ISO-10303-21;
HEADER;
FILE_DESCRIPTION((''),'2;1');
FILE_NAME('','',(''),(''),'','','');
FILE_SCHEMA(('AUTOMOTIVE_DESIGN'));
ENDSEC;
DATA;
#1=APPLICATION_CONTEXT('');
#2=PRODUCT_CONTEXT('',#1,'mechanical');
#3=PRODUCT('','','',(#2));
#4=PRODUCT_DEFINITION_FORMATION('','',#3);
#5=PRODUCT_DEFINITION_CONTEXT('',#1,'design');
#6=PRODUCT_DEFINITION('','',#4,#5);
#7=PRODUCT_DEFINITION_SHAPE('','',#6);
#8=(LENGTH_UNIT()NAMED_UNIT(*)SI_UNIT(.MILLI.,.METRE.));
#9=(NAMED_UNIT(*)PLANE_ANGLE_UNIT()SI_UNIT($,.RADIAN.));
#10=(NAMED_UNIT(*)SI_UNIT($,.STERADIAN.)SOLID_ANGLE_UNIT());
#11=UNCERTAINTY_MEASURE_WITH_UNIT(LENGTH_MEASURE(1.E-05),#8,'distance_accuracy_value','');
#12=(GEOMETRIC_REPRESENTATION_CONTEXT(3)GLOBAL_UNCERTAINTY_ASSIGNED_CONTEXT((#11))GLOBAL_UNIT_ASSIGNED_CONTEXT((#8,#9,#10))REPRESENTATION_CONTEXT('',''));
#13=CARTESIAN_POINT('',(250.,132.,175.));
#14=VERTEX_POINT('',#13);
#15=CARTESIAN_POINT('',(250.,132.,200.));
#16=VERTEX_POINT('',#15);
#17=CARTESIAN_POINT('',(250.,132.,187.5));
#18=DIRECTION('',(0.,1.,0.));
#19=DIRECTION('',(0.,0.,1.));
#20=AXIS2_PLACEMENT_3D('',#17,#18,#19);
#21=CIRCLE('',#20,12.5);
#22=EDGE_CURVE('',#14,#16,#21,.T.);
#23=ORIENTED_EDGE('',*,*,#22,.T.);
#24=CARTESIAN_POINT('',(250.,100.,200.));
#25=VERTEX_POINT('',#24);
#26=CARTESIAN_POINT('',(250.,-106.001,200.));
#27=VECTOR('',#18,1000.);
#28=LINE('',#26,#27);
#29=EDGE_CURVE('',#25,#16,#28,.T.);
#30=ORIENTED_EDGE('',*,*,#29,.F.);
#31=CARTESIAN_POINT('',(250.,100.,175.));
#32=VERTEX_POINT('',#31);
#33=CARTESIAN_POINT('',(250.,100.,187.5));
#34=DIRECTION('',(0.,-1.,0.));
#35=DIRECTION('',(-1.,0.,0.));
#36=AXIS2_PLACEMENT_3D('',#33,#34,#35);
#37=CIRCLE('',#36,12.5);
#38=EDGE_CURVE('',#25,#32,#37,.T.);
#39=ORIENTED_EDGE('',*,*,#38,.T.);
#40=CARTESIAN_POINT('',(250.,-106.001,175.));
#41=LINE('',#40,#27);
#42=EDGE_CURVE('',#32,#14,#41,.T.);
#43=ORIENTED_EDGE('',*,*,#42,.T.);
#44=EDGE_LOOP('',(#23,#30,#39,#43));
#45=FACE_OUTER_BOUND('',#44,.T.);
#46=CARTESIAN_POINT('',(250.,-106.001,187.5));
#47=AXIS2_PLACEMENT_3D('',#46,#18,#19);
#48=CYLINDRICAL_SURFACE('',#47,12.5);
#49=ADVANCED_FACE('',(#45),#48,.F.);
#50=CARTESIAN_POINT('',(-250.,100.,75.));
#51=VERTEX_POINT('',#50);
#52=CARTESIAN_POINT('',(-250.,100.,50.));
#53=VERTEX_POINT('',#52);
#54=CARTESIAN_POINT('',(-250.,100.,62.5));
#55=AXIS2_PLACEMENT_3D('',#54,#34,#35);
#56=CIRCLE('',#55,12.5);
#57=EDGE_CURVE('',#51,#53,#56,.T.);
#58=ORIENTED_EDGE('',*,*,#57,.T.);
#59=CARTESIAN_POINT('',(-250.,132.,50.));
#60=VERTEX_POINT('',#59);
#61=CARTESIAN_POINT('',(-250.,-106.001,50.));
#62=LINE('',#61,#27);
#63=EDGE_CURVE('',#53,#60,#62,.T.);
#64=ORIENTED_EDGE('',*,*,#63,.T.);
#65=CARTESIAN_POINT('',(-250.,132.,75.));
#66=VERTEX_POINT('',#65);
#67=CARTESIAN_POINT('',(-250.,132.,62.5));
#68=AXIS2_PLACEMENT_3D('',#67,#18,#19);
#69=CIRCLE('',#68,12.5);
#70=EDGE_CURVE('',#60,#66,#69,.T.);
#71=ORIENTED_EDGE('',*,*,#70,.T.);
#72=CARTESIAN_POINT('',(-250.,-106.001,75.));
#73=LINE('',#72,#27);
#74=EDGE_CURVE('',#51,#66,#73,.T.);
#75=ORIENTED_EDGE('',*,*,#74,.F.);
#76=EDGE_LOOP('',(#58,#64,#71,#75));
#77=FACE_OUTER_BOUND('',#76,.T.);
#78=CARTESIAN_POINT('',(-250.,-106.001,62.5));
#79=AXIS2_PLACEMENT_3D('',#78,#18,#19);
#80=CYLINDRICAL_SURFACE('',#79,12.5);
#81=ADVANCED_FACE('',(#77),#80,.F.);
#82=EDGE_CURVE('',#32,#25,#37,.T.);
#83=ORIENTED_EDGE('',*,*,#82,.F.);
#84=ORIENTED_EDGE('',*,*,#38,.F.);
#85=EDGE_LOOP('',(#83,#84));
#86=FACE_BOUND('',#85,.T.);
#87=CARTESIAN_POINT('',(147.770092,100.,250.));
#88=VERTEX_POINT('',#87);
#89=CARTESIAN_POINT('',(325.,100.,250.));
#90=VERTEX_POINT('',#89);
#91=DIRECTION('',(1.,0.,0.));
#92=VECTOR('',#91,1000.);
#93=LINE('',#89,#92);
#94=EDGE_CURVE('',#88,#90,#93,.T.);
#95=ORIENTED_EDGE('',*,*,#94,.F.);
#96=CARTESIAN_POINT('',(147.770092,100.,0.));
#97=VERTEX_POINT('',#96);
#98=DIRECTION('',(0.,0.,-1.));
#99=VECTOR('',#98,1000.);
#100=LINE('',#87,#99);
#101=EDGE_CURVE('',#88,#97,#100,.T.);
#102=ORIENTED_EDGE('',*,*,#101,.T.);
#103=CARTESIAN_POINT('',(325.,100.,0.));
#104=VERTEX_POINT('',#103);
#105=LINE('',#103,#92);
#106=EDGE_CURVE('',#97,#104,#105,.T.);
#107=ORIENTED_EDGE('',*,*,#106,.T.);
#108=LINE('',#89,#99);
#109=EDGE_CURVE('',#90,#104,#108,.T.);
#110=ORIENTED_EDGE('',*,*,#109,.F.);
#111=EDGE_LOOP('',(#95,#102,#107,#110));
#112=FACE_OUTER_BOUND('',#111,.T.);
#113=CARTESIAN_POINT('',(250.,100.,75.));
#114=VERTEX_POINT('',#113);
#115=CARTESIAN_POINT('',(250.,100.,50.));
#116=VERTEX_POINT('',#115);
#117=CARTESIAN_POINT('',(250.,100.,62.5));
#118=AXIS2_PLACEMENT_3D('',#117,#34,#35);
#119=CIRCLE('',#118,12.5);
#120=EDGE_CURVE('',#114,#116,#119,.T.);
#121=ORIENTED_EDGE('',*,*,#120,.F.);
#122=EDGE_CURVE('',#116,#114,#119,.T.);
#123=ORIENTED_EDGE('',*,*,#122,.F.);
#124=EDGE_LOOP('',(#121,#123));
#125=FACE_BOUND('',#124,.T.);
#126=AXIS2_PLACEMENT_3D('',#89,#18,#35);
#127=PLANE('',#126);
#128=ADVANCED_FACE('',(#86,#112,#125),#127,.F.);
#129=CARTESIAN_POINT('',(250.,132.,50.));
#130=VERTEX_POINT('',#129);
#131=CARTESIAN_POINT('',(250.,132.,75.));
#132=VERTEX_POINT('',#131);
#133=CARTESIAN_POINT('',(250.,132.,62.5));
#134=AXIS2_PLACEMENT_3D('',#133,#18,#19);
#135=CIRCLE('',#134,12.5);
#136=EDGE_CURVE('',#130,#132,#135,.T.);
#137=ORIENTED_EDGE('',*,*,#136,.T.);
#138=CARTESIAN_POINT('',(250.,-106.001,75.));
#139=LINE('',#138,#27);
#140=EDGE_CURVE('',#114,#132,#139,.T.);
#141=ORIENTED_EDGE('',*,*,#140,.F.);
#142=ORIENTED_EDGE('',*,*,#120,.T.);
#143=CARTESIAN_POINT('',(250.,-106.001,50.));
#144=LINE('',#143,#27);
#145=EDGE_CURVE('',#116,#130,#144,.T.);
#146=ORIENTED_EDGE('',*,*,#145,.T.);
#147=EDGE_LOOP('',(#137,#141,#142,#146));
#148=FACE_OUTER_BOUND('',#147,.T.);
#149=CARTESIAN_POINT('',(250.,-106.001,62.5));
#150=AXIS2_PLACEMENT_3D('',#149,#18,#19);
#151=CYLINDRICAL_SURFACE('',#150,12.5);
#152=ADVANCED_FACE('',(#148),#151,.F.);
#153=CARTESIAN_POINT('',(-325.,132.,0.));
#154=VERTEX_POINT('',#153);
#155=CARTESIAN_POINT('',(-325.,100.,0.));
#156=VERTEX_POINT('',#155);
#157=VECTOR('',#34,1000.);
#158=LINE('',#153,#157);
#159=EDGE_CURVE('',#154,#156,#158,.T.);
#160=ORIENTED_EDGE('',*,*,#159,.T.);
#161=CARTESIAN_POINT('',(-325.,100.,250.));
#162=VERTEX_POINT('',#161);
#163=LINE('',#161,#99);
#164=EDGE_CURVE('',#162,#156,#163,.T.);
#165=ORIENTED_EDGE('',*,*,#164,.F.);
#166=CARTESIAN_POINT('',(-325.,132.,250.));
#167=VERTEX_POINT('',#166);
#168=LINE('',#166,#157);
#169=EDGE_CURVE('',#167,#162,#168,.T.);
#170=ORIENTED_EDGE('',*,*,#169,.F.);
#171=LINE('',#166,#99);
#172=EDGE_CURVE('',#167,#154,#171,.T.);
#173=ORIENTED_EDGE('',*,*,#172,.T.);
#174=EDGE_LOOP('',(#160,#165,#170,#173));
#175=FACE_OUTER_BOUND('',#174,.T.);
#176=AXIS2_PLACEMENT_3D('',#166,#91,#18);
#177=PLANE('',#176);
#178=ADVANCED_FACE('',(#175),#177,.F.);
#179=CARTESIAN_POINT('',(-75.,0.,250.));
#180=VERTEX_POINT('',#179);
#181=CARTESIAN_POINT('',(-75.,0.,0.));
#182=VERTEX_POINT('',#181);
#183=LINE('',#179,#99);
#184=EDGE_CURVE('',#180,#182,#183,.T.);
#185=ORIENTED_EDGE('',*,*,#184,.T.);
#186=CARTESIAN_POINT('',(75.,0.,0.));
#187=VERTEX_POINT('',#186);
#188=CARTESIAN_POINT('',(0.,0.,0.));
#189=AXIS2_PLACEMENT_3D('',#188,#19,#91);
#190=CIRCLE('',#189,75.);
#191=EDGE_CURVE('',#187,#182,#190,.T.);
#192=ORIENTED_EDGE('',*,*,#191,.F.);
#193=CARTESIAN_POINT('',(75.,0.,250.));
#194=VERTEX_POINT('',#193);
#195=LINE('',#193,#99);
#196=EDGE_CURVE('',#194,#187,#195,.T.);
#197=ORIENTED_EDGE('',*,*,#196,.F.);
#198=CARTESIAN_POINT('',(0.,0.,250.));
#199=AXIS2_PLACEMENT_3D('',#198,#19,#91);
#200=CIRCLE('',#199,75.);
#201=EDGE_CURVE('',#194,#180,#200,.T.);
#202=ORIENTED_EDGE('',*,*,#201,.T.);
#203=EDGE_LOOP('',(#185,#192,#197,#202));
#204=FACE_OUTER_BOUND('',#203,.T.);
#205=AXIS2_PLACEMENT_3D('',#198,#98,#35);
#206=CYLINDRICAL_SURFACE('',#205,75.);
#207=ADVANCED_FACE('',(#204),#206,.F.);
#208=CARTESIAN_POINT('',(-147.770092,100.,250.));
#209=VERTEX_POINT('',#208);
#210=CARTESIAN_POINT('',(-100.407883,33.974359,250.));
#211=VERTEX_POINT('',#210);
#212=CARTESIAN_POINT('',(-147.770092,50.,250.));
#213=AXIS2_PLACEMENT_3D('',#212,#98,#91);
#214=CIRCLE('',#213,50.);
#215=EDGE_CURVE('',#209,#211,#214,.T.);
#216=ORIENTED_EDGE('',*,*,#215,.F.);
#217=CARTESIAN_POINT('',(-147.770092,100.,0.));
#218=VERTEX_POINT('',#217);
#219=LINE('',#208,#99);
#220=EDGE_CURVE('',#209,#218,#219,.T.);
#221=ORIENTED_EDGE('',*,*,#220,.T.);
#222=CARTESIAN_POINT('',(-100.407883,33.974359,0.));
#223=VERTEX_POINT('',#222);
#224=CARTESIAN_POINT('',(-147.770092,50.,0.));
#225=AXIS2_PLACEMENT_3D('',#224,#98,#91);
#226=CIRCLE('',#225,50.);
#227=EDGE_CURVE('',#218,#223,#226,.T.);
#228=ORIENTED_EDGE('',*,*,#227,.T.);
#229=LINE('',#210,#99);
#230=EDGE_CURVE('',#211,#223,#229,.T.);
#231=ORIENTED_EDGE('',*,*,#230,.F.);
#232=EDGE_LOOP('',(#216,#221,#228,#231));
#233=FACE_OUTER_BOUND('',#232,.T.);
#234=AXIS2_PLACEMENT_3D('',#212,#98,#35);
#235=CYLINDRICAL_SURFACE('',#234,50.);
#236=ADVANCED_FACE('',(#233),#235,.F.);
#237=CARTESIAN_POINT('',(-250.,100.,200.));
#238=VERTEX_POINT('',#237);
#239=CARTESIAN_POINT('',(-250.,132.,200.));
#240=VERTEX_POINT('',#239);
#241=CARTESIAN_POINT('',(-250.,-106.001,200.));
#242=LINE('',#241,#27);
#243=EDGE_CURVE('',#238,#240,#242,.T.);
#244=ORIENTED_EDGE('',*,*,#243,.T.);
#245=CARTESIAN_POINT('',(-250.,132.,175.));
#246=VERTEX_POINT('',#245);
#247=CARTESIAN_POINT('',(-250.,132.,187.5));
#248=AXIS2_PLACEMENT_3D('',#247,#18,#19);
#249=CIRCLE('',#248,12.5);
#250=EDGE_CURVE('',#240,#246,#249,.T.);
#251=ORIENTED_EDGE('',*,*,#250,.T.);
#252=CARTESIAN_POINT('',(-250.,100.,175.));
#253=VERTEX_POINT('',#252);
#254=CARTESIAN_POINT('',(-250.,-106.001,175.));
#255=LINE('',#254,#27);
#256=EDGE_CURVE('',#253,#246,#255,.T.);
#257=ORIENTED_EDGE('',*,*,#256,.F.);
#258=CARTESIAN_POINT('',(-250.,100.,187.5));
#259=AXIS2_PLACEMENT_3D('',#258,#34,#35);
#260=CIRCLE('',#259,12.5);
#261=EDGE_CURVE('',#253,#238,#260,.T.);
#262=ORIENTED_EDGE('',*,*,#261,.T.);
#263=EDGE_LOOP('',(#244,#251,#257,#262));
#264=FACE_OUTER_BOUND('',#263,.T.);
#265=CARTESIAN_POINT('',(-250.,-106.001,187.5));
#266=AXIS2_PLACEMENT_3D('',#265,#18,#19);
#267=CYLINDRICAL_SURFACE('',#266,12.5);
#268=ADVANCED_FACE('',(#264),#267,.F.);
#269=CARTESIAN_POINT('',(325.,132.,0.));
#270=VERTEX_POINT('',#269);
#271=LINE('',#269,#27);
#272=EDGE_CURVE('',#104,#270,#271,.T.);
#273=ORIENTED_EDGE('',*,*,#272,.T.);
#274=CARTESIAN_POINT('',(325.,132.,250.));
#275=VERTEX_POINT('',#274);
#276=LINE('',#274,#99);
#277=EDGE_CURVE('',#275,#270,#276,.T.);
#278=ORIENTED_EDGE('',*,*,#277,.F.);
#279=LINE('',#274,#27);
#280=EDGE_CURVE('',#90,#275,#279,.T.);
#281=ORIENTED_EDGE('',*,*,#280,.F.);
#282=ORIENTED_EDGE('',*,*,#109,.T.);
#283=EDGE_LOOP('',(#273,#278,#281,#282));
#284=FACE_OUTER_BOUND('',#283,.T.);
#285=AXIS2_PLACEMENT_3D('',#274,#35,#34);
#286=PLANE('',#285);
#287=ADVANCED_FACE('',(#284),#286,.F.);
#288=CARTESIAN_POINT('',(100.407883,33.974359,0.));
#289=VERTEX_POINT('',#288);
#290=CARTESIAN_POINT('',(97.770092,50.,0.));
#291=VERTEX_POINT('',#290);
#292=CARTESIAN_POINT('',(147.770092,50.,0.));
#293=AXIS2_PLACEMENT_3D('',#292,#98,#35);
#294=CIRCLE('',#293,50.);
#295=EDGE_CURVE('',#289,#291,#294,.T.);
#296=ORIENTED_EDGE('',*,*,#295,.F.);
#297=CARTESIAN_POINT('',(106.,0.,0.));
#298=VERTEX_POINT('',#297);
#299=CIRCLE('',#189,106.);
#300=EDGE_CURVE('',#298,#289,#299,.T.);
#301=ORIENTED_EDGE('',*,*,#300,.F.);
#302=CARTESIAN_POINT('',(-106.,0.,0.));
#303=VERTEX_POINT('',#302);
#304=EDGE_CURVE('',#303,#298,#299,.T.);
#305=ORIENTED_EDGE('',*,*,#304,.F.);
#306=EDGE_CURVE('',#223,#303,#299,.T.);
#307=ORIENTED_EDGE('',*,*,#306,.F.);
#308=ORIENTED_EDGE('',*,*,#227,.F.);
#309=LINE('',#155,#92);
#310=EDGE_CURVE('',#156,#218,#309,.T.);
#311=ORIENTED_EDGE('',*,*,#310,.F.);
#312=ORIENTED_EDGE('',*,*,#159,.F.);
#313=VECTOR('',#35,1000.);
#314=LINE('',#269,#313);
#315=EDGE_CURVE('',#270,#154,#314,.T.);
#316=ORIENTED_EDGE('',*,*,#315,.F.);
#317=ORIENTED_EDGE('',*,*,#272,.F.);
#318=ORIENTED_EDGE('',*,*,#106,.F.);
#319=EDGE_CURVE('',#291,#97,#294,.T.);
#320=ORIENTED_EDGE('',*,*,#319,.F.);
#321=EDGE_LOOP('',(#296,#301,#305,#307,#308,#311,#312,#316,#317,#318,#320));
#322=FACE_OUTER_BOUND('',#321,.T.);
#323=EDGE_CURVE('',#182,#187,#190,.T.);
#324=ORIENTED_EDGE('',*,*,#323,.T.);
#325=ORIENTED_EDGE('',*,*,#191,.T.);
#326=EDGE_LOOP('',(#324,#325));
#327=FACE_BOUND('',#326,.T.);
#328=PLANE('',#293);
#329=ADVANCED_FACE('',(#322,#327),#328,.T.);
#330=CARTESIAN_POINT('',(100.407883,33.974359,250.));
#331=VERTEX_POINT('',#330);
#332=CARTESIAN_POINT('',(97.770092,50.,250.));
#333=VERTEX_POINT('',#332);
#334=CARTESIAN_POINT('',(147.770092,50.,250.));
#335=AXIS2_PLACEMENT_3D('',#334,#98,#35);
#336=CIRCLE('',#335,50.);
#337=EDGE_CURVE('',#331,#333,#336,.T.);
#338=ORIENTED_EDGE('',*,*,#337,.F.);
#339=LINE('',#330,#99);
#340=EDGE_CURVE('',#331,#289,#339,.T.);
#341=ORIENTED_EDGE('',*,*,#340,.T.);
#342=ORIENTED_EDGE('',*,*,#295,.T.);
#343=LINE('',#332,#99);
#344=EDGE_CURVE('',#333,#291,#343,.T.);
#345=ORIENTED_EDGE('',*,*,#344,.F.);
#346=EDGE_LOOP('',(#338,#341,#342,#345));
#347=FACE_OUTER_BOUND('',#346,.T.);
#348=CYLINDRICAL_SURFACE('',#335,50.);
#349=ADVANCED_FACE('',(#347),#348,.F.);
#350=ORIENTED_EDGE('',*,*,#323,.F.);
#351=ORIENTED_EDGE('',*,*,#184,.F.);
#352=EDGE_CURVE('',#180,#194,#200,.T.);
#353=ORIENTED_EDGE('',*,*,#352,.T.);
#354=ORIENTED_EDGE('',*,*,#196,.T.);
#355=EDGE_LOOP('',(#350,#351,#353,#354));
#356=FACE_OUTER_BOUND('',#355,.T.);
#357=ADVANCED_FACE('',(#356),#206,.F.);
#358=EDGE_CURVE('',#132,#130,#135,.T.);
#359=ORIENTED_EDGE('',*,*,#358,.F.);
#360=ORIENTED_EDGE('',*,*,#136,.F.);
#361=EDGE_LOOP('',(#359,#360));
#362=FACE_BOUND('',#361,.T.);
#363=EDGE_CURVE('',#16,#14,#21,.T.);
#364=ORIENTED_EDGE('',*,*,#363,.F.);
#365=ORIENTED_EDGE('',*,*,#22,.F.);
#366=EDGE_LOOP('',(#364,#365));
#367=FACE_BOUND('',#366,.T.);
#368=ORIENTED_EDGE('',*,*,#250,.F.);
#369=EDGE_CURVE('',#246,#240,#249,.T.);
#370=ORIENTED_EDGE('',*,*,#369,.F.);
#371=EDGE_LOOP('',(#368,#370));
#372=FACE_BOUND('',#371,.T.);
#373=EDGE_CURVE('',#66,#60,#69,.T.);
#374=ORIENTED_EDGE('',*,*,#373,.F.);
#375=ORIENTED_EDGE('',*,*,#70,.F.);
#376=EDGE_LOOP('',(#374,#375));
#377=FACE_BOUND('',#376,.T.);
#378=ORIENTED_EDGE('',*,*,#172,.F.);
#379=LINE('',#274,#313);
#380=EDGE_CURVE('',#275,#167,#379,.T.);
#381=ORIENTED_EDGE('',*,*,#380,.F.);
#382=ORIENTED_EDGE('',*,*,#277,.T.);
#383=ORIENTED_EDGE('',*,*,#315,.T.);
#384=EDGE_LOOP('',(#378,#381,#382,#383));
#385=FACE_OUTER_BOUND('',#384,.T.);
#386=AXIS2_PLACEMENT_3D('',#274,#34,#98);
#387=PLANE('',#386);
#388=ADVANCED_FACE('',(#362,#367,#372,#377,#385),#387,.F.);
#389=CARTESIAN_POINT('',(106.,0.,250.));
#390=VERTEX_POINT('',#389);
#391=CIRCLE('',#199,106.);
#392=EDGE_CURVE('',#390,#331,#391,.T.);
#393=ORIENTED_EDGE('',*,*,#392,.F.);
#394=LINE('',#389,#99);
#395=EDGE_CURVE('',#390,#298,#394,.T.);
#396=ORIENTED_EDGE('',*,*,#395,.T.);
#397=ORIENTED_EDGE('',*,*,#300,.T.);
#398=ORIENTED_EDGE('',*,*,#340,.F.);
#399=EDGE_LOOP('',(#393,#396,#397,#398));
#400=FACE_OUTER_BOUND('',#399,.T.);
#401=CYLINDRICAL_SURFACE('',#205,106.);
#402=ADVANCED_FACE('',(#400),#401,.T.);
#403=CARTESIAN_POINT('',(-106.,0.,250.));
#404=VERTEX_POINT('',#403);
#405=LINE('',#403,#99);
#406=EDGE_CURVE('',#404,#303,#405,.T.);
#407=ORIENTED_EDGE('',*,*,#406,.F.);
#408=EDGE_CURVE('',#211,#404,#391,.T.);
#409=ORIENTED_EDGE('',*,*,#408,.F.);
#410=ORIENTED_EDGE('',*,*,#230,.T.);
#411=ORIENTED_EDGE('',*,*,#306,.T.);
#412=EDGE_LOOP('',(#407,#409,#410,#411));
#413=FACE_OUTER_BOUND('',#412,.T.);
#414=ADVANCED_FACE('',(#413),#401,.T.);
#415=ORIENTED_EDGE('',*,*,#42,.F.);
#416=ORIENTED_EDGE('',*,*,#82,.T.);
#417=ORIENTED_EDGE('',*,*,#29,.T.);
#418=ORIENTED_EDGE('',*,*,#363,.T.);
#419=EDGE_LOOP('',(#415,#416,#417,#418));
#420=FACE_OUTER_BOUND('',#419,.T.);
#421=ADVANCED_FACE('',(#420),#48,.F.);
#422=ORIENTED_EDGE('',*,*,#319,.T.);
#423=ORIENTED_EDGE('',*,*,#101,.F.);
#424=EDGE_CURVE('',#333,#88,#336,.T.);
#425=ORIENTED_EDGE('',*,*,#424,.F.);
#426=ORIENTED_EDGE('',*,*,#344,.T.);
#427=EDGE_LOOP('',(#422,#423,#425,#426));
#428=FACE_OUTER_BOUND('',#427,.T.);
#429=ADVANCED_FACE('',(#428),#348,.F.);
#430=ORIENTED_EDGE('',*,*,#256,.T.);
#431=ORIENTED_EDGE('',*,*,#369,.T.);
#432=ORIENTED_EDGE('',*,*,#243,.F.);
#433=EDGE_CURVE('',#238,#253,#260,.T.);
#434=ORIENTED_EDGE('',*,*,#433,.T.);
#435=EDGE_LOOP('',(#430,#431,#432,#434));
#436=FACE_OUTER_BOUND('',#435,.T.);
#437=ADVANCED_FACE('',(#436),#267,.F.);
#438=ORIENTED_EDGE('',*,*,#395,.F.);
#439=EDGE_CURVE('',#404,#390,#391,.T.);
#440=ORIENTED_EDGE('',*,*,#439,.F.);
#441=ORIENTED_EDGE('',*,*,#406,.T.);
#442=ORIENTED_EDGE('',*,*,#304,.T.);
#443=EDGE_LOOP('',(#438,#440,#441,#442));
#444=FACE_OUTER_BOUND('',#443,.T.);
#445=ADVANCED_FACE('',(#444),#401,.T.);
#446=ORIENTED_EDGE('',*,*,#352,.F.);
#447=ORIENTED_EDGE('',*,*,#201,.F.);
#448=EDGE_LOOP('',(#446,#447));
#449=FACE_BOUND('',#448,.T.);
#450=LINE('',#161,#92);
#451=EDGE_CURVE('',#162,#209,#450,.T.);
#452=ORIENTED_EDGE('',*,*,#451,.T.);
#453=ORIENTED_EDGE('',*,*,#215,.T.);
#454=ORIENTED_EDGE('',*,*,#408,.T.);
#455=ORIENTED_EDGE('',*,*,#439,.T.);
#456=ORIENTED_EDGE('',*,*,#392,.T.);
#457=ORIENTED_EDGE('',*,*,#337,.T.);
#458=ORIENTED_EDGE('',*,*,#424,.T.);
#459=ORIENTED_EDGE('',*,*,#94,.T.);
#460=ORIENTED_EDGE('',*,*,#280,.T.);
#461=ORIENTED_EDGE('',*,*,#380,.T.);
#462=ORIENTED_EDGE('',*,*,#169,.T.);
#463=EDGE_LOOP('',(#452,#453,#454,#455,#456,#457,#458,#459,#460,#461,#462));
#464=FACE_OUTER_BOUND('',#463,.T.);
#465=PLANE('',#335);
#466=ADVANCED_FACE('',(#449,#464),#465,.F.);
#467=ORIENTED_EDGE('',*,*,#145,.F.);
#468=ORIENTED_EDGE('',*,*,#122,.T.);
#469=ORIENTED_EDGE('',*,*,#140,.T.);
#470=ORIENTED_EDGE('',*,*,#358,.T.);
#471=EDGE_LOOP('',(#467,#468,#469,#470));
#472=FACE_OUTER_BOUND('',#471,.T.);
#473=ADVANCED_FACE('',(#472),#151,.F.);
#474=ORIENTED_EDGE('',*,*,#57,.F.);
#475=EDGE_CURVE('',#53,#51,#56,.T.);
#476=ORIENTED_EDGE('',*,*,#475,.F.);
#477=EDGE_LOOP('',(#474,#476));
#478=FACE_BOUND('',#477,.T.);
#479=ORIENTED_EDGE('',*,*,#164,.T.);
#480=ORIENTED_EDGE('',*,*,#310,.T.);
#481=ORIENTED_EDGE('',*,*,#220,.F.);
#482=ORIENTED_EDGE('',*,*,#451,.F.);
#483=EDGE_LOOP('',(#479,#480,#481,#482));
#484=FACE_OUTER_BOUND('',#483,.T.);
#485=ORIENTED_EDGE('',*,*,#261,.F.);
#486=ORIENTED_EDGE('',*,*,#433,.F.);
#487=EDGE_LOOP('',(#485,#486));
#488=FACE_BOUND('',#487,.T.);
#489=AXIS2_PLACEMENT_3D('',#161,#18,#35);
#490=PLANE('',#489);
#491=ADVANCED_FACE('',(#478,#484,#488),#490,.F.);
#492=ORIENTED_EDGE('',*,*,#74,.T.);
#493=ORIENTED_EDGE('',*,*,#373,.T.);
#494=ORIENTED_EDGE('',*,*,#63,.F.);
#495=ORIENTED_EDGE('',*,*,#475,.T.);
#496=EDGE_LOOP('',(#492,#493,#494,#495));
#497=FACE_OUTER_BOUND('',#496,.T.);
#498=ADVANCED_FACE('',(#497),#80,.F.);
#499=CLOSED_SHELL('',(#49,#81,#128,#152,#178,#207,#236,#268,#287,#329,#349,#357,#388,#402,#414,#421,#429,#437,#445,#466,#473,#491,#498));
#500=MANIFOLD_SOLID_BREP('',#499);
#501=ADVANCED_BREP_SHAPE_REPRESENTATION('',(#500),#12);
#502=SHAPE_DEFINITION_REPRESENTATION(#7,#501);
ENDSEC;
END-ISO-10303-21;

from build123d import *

# Parameters (mm, degrees)
SKETCH1_R           = 75
BOSS_EXTRUDE1_DEPTH = 250
CUT_EXTRUDE1_REACH  = 476.098
SKETCH2_R           = 12.5


with BuildPart() as part:
    # Sketch1 → Boss-Extrude1 (new body)
    with BuildSketch(Plane.XY):
        with BuildLine():
            Line((325, 132), (-325, 132))
            Line((-325, 132), (-325, 100))
            Line((-325, 100), (-147.770091697, 100))
            ThreePointArc((-147.770091697, 100), (-107.142009959, 79.143763902), (-100.407882819, 33.974358974))
            ThreePointArc((-100.407882819, 33.974358974), (0, -106), (100.407882819, 33.974358974))
            ThreePointArc((100.407882819, 33.974358974), (107.142009959, 79.143763902), (147.770091697, 100))
            Line((147.770091697, 100), (325, 100))
            Line((325, 100), (325, 132))
        make_face()
        Circle(SKETCH1_R, mode=Mode.SUBTRACT)
    extrude(amount=BOSS_EXTRUDE1_DEPTH)

    # Sketch2 → Cut-Extrude1 (cut, up to next)
    with BuildSketch(Plane(origin=(0, 132, 0), x_dir=(1, 0, 0), z_dir=(0, 1, 0)), mode=Mode.PRIVATE) as cut_extrude1_sk1:
        with Locations(Location((-250, -62.5, 0), (0, 0, 270))):
            Circle(SKETCH2_R)
    cut_extrude1_tool1 = extrude(cut_extrude1_sk1.sketch, amount=-CUT_EXTRUDE1_REACH, mode=Mode.PRIVATE) & part.part
    # Sketch2 → Cut-Extrude1 (cut, up to next)
    with BuildSketch(Plane(origin=(0, 132, 0), x_dir=(1, 0, 0), z_dir=(0, 1, 0)), mode=Mode.PRIVATE) as cut_extrude1_sk2:
        with Locations(Location((-250, -187.5, 0), (0, 0, 270))):
            Circle(SKETCH2_R)
    cut_extrude1_tool2 = extrude(cut_extrude1_sk2.sketch, amount=-CUT_EXTRUDE1_REACH, mode=Mode.PRIVATE) & part.part
    # Sketch2 → Cut-Extrude1 (cut, up to next)
    with BuildSketch(Plane(origin=(0, 132, 0), x_dir=(1, 0, 0), z_dir=(0, 1, 0)), mode=Mode.PRIVATE) as cut_extrude1_sk3:
        with Locations(Location((250, -187.5, 0), (0, 0, 270))):
            Circle(SKETCH2_R)
    cut_extrude1_tool3 = extrude(cut_extrude1_sk3.sketch, amount=-CUT_EXTRUDE1_REACH, mode=Mode.PRIVATE) & part.part
    # Sketch2 → Cut-Extrude1 (cut, up to next)
    with BuildSketch(Plane(origin=(0, 132, 0), x_dir=(1, 0, 0), z_dir=(0, 1, 0)), mode=Mode.PRIVATE) as cut_extrude1_sk4:
        with Locations(Location((250, -62.5, 0), (0, 0, 270))):
            Circle(SKETCH2_R)
    cut_extrude1_tool4 = extrude(cut_extrude1_sk4.sketch, amount=-CUT_EXTRUDE1_REACH, mode=Mode.PRIVATE) & part.part
    add(cut_extrude1_tool1.solids().sort_by_distance((-250, 132, 62.5))[0], mode=Mode.SUBTRACT)
    add(cut_extrude1_tool2.solids().sort_by_distance((-250, 132, 187.5))[0], mode=Mode.SUBTRACT)
    add(cut_extrude1_tool3.solids().sort_by_distance((250, 132, 187.5))[0], mode=Mode.SUBTRACT)
    add(cut_extrude1_tool4.solids().sort_by_distance((250, 132, 62.5))[0], mode=Mode.SUBTRACT)


solid = part.part
